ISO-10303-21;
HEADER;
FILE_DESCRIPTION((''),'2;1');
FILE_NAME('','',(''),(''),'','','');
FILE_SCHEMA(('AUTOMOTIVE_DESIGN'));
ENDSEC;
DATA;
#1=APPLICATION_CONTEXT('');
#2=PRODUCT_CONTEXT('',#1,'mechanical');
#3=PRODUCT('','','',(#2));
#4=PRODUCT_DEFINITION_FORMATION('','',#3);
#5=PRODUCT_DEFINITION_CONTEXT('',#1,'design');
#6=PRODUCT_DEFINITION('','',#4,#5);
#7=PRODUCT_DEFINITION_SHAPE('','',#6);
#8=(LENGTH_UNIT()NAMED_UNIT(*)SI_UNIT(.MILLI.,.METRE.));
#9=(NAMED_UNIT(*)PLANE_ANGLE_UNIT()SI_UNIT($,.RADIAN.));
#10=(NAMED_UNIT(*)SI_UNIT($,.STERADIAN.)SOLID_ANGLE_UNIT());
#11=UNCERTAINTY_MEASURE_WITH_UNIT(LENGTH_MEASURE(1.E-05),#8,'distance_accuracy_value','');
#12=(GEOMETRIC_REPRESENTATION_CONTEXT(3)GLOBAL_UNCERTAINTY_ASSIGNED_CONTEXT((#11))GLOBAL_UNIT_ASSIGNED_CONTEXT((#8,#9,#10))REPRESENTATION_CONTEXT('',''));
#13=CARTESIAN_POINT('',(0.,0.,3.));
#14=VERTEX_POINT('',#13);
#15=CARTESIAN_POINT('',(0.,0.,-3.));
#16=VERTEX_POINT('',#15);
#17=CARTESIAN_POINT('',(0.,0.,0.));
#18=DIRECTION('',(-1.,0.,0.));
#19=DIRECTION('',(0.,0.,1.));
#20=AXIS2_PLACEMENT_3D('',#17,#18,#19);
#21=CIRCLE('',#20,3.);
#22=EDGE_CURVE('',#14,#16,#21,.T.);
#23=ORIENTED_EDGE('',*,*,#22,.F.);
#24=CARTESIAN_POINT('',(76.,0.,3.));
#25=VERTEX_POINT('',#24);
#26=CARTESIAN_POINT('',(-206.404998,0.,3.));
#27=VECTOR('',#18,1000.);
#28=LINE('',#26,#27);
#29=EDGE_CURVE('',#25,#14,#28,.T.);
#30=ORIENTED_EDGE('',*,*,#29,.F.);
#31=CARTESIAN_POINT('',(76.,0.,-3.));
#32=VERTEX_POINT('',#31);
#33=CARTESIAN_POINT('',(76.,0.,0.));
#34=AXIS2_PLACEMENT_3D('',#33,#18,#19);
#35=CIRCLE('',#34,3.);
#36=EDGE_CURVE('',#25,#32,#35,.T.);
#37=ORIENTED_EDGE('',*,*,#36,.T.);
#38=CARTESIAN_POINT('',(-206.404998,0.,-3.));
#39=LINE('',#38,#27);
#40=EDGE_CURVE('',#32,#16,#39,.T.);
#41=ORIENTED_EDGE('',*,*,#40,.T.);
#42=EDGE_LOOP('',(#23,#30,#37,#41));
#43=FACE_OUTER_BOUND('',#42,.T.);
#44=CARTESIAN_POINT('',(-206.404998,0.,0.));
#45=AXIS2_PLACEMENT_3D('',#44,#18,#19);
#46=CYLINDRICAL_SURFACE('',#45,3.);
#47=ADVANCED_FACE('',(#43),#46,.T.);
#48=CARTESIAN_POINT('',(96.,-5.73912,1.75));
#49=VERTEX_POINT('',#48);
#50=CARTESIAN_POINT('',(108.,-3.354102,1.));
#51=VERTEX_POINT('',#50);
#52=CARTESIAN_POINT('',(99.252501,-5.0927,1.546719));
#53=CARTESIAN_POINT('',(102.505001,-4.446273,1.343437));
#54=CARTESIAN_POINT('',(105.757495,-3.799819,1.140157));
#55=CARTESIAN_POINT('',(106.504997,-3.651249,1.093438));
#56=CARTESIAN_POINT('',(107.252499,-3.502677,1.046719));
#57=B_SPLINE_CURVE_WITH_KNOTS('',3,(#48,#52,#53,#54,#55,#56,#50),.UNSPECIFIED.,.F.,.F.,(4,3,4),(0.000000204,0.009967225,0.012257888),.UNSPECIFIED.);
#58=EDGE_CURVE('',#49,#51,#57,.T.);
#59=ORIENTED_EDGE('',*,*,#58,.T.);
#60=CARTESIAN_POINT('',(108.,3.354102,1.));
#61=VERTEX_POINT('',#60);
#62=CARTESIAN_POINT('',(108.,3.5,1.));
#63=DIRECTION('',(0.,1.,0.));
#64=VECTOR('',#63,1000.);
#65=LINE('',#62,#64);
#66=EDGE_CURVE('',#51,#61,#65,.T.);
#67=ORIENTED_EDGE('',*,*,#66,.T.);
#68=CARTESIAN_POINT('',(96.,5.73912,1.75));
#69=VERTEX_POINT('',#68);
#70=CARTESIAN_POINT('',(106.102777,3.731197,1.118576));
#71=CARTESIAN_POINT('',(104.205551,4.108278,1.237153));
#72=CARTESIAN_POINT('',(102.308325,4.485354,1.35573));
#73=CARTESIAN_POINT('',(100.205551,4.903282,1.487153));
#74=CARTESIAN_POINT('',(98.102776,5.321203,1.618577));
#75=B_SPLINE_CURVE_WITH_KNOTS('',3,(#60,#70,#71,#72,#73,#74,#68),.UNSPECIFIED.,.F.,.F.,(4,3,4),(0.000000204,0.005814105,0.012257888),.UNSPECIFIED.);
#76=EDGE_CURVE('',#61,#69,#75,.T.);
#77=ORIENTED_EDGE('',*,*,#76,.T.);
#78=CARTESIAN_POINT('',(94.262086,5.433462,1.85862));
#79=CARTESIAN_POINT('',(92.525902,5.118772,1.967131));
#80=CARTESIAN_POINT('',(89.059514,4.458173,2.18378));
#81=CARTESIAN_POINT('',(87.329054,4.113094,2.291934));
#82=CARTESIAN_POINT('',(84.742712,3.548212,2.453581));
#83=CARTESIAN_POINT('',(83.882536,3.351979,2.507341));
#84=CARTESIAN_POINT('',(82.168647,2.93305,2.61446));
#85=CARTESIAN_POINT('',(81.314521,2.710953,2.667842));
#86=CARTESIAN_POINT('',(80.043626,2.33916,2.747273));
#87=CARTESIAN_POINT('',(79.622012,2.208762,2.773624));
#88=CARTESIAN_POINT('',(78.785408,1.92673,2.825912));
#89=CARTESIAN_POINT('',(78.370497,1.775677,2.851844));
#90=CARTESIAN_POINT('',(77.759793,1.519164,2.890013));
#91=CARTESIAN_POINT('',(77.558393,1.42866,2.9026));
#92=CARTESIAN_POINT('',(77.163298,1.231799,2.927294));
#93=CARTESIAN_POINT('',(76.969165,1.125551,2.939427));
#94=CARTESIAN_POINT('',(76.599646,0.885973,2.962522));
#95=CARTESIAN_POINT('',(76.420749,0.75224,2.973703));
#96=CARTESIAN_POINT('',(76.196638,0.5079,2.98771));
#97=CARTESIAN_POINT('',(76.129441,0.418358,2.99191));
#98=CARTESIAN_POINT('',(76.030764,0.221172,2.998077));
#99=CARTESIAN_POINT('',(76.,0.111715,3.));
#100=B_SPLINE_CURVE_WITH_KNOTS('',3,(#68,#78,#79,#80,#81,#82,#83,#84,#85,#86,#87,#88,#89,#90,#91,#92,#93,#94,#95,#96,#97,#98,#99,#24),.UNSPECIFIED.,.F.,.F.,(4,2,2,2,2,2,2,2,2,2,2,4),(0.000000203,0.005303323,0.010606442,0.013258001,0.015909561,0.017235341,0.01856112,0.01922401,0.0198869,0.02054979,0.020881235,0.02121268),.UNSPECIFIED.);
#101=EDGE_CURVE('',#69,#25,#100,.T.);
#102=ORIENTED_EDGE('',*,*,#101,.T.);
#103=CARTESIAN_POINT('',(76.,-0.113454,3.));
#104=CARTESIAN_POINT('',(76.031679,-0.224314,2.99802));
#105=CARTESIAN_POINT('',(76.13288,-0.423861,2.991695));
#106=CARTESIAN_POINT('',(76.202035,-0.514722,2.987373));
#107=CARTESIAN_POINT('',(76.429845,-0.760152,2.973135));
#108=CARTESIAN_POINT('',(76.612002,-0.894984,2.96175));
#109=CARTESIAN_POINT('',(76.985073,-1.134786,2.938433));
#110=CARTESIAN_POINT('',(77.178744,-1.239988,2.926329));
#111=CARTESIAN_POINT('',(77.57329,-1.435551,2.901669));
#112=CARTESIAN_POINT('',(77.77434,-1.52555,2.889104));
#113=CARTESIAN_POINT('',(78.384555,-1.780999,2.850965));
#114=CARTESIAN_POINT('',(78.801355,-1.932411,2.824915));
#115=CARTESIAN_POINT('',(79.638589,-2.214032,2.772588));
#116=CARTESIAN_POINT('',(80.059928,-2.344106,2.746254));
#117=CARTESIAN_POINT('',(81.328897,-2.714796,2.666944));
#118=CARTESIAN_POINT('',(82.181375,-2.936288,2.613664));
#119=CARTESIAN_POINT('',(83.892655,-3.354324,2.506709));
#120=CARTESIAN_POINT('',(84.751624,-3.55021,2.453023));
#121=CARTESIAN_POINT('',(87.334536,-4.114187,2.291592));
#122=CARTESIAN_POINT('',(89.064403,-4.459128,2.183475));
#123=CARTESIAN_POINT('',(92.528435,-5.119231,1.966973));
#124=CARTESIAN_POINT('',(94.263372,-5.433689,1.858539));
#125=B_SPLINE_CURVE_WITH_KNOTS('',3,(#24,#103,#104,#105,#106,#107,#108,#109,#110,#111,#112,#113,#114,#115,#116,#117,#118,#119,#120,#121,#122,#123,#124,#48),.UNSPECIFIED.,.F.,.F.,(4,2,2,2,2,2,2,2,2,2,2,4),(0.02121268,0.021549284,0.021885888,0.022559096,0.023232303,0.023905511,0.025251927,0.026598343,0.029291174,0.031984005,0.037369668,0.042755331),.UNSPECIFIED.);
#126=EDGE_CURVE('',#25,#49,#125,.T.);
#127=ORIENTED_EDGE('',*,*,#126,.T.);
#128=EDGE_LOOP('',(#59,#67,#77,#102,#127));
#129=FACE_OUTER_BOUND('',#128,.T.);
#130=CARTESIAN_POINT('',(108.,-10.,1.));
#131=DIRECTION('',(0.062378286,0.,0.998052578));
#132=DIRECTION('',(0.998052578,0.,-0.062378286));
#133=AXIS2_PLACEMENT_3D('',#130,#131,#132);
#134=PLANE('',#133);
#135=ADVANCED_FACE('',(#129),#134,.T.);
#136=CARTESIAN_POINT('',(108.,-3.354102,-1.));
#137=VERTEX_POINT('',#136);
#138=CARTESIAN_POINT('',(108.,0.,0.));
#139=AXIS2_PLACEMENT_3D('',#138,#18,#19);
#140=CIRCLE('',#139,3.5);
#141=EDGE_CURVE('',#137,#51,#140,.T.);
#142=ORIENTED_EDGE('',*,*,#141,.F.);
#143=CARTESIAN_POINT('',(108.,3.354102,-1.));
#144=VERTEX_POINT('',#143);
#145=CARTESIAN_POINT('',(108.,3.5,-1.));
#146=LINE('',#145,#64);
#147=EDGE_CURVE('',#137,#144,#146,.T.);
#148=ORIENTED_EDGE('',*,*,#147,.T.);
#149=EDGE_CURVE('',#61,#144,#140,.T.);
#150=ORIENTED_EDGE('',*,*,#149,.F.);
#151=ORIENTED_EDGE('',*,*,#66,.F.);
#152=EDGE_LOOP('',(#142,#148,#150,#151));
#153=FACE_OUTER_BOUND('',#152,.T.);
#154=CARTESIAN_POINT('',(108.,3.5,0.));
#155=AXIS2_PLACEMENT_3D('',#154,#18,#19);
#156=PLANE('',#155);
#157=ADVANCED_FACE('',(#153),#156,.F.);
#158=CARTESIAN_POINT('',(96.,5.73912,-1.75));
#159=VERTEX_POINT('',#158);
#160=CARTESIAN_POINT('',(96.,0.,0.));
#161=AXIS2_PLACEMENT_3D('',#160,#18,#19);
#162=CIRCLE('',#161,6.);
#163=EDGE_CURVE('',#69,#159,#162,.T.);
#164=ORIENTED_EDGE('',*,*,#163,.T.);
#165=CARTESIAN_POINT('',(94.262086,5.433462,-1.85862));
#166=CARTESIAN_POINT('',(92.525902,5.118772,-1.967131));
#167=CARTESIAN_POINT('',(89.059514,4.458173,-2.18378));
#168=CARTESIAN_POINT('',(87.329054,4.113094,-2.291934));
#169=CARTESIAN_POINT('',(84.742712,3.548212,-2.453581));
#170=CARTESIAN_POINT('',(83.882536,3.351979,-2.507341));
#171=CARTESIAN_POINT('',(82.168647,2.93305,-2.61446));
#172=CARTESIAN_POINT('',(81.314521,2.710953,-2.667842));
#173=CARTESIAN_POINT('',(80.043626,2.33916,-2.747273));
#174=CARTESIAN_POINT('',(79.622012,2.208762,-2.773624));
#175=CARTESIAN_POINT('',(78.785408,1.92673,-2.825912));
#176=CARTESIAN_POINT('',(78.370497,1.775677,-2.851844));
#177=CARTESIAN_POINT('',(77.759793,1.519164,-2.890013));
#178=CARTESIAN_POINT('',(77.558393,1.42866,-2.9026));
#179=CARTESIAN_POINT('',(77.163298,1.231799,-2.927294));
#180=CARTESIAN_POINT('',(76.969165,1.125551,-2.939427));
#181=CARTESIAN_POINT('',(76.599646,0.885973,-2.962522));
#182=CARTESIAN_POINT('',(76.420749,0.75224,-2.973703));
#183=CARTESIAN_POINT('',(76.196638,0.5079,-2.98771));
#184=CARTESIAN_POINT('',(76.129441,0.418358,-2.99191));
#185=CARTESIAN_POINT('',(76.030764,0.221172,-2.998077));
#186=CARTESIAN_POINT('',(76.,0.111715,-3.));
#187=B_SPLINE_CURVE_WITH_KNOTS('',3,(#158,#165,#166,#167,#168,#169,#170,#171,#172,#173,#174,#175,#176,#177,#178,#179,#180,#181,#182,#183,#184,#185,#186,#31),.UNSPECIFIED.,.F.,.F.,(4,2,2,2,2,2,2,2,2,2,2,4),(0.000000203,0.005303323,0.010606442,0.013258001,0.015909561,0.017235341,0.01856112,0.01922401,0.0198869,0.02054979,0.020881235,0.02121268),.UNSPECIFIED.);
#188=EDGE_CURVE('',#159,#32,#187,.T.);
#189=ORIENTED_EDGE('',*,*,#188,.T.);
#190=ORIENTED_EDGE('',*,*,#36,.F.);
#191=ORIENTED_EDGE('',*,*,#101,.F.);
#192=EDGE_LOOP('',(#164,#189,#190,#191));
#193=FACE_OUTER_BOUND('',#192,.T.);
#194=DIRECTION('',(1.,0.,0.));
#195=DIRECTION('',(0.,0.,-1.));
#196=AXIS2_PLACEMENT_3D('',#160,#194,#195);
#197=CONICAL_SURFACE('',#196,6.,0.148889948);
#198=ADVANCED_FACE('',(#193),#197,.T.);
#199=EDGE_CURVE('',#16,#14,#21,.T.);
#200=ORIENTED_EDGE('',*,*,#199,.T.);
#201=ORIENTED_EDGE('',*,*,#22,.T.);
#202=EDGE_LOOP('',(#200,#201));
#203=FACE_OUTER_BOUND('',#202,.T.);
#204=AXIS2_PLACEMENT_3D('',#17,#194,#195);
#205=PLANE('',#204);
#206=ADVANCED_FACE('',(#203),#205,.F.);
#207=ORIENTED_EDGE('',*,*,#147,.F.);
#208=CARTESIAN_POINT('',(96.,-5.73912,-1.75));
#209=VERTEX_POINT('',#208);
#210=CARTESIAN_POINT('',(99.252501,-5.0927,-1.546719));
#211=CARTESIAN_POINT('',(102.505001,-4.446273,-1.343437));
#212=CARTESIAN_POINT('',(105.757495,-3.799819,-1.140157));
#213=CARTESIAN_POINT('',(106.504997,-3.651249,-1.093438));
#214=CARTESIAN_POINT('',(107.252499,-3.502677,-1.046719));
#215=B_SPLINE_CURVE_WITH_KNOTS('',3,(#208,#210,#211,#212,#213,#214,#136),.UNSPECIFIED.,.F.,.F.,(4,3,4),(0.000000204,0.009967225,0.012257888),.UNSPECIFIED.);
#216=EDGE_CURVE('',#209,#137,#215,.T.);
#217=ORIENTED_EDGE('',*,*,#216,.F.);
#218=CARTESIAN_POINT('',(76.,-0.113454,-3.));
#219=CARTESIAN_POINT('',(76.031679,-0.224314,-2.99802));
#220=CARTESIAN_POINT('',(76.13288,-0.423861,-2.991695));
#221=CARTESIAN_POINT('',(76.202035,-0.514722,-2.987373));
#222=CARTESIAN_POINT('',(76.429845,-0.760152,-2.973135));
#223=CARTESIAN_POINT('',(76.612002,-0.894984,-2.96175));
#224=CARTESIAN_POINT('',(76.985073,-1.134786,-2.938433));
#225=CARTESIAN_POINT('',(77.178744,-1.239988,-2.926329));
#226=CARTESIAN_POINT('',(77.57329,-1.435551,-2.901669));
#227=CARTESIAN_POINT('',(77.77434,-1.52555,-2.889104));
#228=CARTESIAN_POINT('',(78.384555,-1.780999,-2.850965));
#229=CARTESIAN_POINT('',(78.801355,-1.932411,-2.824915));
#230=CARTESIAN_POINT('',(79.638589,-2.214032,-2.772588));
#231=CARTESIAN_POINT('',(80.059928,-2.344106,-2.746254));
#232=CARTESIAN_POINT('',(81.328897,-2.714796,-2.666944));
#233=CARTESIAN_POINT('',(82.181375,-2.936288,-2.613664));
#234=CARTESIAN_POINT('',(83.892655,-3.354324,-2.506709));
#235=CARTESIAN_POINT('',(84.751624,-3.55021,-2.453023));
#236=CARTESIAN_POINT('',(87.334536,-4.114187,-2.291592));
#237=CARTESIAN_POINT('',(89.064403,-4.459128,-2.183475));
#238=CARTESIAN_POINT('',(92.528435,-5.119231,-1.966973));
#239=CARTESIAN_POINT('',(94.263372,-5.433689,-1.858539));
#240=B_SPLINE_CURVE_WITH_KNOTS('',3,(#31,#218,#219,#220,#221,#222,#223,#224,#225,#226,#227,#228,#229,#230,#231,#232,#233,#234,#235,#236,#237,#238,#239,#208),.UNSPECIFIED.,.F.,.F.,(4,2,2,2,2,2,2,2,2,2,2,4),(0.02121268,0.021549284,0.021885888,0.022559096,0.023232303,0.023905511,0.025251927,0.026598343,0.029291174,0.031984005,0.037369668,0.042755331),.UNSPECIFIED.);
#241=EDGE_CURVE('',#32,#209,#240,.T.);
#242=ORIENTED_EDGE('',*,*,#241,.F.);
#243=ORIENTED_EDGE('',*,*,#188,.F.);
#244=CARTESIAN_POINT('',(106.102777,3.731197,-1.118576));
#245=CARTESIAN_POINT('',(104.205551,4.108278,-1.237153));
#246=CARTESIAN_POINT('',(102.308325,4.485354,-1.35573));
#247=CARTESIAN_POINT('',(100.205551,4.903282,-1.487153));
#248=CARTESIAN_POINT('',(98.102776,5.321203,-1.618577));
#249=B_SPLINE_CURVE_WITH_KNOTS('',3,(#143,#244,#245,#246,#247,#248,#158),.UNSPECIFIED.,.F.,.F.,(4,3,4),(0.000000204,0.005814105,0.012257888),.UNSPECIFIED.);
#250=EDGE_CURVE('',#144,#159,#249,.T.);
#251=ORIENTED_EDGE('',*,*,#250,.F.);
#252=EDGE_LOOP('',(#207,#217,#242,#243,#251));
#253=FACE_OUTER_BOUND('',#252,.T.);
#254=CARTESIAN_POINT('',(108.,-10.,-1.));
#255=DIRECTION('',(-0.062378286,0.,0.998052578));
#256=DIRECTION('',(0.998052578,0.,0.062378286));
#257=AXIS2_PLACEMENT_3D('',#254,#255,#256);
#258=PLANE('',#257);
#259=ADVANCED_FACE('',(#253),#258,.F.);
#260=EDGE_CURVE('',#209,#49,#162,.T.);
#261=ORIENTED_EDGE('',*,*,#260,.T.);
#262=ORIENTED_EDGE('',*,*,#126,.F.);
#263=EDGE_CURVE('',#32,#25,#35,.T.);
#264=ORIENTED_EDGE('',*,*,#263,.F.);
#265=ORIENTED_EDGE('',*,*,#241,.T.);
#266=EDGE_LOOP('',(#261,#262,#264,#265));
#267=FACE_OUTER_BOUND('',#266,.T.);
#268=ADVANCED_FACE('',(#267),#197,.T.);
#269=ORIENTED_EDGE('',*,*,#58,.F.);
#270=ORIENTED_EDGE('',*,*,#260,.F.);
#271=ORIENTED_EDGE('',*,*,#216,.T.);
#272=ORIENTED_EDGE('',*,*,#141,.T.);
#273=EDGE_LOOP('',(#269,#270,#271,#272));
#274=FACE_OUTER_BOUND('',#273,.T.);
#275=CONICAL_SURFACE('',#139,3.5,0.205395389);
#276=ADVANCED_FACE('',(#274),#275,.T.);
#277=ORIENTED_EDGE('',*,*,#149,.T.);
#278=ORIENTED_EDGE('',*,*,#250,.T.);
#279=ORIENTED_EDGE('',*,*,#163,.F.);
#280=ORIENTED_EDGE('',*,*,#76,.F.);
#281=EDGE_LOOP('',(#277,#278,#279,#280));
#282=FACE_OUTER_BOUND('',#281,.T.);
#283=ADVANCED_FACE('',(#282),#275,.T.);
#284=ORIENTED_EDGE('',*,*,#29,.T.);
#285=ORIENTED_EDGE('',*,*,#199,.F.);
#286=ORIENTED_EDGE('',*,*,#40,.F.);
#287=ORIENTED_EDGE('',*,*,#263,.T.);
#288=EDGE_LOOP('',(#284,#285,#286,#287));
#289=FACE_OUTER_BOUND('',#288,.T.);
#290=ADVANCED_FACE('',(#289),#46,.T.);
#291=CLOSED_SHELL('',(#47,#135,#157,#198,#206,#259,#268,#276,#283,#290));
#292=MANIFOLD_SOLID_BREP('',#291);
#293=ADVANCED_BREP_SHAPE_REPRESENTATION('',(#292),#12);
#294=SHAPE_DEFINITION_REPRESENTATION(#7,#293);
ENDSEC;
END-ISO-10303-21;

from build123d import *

# Parameters (mm, degrees)
BLADE_FLAT_CUT_DEPTH = 10


with BuildPart() as part:
    # Shaft Profile Sketch → Shaft Revolve (revolve)
    with BuildSketch(Plane.XY, mode=Mode.PRIVATE) as shaft_revolve_sk:
        Polygon((0, 0), (0, 3), (76, 3), (96, 6), (108, 3.5), (108, 0), align=None)
    revolve(shaft_revolve_sk.sketch.rotate(Axis((-206.404998063, 0, 0), (1, 0, 0)), 90), axis=Axis((-206.404998063, 0, 0), (1, 0, 0)))

    # Blade Flat Sketch → Blade Flat Cut (cut, symmetric)
    with BuildSketch(Plane(origin=(0, 0, 0), x_dir=(1, 0, 0), z_dir=(0, 1, 0))):
        Polygon((108, 1), (76, 3), (76, 10.728035522), (108, 10.728035522), align=None)
    blade_flat_cut = extrude(amount=BLADE_FLAT_CUT_DEPTH, both=True, mode=Mode.SUBTRACT)

    # Blade Flat Mirror: Blade Flat Cut across plane
    add(blade_flat_cut.mirror(Plane.XY), mode=Mode.SUBTRACT)


solid = part.part
